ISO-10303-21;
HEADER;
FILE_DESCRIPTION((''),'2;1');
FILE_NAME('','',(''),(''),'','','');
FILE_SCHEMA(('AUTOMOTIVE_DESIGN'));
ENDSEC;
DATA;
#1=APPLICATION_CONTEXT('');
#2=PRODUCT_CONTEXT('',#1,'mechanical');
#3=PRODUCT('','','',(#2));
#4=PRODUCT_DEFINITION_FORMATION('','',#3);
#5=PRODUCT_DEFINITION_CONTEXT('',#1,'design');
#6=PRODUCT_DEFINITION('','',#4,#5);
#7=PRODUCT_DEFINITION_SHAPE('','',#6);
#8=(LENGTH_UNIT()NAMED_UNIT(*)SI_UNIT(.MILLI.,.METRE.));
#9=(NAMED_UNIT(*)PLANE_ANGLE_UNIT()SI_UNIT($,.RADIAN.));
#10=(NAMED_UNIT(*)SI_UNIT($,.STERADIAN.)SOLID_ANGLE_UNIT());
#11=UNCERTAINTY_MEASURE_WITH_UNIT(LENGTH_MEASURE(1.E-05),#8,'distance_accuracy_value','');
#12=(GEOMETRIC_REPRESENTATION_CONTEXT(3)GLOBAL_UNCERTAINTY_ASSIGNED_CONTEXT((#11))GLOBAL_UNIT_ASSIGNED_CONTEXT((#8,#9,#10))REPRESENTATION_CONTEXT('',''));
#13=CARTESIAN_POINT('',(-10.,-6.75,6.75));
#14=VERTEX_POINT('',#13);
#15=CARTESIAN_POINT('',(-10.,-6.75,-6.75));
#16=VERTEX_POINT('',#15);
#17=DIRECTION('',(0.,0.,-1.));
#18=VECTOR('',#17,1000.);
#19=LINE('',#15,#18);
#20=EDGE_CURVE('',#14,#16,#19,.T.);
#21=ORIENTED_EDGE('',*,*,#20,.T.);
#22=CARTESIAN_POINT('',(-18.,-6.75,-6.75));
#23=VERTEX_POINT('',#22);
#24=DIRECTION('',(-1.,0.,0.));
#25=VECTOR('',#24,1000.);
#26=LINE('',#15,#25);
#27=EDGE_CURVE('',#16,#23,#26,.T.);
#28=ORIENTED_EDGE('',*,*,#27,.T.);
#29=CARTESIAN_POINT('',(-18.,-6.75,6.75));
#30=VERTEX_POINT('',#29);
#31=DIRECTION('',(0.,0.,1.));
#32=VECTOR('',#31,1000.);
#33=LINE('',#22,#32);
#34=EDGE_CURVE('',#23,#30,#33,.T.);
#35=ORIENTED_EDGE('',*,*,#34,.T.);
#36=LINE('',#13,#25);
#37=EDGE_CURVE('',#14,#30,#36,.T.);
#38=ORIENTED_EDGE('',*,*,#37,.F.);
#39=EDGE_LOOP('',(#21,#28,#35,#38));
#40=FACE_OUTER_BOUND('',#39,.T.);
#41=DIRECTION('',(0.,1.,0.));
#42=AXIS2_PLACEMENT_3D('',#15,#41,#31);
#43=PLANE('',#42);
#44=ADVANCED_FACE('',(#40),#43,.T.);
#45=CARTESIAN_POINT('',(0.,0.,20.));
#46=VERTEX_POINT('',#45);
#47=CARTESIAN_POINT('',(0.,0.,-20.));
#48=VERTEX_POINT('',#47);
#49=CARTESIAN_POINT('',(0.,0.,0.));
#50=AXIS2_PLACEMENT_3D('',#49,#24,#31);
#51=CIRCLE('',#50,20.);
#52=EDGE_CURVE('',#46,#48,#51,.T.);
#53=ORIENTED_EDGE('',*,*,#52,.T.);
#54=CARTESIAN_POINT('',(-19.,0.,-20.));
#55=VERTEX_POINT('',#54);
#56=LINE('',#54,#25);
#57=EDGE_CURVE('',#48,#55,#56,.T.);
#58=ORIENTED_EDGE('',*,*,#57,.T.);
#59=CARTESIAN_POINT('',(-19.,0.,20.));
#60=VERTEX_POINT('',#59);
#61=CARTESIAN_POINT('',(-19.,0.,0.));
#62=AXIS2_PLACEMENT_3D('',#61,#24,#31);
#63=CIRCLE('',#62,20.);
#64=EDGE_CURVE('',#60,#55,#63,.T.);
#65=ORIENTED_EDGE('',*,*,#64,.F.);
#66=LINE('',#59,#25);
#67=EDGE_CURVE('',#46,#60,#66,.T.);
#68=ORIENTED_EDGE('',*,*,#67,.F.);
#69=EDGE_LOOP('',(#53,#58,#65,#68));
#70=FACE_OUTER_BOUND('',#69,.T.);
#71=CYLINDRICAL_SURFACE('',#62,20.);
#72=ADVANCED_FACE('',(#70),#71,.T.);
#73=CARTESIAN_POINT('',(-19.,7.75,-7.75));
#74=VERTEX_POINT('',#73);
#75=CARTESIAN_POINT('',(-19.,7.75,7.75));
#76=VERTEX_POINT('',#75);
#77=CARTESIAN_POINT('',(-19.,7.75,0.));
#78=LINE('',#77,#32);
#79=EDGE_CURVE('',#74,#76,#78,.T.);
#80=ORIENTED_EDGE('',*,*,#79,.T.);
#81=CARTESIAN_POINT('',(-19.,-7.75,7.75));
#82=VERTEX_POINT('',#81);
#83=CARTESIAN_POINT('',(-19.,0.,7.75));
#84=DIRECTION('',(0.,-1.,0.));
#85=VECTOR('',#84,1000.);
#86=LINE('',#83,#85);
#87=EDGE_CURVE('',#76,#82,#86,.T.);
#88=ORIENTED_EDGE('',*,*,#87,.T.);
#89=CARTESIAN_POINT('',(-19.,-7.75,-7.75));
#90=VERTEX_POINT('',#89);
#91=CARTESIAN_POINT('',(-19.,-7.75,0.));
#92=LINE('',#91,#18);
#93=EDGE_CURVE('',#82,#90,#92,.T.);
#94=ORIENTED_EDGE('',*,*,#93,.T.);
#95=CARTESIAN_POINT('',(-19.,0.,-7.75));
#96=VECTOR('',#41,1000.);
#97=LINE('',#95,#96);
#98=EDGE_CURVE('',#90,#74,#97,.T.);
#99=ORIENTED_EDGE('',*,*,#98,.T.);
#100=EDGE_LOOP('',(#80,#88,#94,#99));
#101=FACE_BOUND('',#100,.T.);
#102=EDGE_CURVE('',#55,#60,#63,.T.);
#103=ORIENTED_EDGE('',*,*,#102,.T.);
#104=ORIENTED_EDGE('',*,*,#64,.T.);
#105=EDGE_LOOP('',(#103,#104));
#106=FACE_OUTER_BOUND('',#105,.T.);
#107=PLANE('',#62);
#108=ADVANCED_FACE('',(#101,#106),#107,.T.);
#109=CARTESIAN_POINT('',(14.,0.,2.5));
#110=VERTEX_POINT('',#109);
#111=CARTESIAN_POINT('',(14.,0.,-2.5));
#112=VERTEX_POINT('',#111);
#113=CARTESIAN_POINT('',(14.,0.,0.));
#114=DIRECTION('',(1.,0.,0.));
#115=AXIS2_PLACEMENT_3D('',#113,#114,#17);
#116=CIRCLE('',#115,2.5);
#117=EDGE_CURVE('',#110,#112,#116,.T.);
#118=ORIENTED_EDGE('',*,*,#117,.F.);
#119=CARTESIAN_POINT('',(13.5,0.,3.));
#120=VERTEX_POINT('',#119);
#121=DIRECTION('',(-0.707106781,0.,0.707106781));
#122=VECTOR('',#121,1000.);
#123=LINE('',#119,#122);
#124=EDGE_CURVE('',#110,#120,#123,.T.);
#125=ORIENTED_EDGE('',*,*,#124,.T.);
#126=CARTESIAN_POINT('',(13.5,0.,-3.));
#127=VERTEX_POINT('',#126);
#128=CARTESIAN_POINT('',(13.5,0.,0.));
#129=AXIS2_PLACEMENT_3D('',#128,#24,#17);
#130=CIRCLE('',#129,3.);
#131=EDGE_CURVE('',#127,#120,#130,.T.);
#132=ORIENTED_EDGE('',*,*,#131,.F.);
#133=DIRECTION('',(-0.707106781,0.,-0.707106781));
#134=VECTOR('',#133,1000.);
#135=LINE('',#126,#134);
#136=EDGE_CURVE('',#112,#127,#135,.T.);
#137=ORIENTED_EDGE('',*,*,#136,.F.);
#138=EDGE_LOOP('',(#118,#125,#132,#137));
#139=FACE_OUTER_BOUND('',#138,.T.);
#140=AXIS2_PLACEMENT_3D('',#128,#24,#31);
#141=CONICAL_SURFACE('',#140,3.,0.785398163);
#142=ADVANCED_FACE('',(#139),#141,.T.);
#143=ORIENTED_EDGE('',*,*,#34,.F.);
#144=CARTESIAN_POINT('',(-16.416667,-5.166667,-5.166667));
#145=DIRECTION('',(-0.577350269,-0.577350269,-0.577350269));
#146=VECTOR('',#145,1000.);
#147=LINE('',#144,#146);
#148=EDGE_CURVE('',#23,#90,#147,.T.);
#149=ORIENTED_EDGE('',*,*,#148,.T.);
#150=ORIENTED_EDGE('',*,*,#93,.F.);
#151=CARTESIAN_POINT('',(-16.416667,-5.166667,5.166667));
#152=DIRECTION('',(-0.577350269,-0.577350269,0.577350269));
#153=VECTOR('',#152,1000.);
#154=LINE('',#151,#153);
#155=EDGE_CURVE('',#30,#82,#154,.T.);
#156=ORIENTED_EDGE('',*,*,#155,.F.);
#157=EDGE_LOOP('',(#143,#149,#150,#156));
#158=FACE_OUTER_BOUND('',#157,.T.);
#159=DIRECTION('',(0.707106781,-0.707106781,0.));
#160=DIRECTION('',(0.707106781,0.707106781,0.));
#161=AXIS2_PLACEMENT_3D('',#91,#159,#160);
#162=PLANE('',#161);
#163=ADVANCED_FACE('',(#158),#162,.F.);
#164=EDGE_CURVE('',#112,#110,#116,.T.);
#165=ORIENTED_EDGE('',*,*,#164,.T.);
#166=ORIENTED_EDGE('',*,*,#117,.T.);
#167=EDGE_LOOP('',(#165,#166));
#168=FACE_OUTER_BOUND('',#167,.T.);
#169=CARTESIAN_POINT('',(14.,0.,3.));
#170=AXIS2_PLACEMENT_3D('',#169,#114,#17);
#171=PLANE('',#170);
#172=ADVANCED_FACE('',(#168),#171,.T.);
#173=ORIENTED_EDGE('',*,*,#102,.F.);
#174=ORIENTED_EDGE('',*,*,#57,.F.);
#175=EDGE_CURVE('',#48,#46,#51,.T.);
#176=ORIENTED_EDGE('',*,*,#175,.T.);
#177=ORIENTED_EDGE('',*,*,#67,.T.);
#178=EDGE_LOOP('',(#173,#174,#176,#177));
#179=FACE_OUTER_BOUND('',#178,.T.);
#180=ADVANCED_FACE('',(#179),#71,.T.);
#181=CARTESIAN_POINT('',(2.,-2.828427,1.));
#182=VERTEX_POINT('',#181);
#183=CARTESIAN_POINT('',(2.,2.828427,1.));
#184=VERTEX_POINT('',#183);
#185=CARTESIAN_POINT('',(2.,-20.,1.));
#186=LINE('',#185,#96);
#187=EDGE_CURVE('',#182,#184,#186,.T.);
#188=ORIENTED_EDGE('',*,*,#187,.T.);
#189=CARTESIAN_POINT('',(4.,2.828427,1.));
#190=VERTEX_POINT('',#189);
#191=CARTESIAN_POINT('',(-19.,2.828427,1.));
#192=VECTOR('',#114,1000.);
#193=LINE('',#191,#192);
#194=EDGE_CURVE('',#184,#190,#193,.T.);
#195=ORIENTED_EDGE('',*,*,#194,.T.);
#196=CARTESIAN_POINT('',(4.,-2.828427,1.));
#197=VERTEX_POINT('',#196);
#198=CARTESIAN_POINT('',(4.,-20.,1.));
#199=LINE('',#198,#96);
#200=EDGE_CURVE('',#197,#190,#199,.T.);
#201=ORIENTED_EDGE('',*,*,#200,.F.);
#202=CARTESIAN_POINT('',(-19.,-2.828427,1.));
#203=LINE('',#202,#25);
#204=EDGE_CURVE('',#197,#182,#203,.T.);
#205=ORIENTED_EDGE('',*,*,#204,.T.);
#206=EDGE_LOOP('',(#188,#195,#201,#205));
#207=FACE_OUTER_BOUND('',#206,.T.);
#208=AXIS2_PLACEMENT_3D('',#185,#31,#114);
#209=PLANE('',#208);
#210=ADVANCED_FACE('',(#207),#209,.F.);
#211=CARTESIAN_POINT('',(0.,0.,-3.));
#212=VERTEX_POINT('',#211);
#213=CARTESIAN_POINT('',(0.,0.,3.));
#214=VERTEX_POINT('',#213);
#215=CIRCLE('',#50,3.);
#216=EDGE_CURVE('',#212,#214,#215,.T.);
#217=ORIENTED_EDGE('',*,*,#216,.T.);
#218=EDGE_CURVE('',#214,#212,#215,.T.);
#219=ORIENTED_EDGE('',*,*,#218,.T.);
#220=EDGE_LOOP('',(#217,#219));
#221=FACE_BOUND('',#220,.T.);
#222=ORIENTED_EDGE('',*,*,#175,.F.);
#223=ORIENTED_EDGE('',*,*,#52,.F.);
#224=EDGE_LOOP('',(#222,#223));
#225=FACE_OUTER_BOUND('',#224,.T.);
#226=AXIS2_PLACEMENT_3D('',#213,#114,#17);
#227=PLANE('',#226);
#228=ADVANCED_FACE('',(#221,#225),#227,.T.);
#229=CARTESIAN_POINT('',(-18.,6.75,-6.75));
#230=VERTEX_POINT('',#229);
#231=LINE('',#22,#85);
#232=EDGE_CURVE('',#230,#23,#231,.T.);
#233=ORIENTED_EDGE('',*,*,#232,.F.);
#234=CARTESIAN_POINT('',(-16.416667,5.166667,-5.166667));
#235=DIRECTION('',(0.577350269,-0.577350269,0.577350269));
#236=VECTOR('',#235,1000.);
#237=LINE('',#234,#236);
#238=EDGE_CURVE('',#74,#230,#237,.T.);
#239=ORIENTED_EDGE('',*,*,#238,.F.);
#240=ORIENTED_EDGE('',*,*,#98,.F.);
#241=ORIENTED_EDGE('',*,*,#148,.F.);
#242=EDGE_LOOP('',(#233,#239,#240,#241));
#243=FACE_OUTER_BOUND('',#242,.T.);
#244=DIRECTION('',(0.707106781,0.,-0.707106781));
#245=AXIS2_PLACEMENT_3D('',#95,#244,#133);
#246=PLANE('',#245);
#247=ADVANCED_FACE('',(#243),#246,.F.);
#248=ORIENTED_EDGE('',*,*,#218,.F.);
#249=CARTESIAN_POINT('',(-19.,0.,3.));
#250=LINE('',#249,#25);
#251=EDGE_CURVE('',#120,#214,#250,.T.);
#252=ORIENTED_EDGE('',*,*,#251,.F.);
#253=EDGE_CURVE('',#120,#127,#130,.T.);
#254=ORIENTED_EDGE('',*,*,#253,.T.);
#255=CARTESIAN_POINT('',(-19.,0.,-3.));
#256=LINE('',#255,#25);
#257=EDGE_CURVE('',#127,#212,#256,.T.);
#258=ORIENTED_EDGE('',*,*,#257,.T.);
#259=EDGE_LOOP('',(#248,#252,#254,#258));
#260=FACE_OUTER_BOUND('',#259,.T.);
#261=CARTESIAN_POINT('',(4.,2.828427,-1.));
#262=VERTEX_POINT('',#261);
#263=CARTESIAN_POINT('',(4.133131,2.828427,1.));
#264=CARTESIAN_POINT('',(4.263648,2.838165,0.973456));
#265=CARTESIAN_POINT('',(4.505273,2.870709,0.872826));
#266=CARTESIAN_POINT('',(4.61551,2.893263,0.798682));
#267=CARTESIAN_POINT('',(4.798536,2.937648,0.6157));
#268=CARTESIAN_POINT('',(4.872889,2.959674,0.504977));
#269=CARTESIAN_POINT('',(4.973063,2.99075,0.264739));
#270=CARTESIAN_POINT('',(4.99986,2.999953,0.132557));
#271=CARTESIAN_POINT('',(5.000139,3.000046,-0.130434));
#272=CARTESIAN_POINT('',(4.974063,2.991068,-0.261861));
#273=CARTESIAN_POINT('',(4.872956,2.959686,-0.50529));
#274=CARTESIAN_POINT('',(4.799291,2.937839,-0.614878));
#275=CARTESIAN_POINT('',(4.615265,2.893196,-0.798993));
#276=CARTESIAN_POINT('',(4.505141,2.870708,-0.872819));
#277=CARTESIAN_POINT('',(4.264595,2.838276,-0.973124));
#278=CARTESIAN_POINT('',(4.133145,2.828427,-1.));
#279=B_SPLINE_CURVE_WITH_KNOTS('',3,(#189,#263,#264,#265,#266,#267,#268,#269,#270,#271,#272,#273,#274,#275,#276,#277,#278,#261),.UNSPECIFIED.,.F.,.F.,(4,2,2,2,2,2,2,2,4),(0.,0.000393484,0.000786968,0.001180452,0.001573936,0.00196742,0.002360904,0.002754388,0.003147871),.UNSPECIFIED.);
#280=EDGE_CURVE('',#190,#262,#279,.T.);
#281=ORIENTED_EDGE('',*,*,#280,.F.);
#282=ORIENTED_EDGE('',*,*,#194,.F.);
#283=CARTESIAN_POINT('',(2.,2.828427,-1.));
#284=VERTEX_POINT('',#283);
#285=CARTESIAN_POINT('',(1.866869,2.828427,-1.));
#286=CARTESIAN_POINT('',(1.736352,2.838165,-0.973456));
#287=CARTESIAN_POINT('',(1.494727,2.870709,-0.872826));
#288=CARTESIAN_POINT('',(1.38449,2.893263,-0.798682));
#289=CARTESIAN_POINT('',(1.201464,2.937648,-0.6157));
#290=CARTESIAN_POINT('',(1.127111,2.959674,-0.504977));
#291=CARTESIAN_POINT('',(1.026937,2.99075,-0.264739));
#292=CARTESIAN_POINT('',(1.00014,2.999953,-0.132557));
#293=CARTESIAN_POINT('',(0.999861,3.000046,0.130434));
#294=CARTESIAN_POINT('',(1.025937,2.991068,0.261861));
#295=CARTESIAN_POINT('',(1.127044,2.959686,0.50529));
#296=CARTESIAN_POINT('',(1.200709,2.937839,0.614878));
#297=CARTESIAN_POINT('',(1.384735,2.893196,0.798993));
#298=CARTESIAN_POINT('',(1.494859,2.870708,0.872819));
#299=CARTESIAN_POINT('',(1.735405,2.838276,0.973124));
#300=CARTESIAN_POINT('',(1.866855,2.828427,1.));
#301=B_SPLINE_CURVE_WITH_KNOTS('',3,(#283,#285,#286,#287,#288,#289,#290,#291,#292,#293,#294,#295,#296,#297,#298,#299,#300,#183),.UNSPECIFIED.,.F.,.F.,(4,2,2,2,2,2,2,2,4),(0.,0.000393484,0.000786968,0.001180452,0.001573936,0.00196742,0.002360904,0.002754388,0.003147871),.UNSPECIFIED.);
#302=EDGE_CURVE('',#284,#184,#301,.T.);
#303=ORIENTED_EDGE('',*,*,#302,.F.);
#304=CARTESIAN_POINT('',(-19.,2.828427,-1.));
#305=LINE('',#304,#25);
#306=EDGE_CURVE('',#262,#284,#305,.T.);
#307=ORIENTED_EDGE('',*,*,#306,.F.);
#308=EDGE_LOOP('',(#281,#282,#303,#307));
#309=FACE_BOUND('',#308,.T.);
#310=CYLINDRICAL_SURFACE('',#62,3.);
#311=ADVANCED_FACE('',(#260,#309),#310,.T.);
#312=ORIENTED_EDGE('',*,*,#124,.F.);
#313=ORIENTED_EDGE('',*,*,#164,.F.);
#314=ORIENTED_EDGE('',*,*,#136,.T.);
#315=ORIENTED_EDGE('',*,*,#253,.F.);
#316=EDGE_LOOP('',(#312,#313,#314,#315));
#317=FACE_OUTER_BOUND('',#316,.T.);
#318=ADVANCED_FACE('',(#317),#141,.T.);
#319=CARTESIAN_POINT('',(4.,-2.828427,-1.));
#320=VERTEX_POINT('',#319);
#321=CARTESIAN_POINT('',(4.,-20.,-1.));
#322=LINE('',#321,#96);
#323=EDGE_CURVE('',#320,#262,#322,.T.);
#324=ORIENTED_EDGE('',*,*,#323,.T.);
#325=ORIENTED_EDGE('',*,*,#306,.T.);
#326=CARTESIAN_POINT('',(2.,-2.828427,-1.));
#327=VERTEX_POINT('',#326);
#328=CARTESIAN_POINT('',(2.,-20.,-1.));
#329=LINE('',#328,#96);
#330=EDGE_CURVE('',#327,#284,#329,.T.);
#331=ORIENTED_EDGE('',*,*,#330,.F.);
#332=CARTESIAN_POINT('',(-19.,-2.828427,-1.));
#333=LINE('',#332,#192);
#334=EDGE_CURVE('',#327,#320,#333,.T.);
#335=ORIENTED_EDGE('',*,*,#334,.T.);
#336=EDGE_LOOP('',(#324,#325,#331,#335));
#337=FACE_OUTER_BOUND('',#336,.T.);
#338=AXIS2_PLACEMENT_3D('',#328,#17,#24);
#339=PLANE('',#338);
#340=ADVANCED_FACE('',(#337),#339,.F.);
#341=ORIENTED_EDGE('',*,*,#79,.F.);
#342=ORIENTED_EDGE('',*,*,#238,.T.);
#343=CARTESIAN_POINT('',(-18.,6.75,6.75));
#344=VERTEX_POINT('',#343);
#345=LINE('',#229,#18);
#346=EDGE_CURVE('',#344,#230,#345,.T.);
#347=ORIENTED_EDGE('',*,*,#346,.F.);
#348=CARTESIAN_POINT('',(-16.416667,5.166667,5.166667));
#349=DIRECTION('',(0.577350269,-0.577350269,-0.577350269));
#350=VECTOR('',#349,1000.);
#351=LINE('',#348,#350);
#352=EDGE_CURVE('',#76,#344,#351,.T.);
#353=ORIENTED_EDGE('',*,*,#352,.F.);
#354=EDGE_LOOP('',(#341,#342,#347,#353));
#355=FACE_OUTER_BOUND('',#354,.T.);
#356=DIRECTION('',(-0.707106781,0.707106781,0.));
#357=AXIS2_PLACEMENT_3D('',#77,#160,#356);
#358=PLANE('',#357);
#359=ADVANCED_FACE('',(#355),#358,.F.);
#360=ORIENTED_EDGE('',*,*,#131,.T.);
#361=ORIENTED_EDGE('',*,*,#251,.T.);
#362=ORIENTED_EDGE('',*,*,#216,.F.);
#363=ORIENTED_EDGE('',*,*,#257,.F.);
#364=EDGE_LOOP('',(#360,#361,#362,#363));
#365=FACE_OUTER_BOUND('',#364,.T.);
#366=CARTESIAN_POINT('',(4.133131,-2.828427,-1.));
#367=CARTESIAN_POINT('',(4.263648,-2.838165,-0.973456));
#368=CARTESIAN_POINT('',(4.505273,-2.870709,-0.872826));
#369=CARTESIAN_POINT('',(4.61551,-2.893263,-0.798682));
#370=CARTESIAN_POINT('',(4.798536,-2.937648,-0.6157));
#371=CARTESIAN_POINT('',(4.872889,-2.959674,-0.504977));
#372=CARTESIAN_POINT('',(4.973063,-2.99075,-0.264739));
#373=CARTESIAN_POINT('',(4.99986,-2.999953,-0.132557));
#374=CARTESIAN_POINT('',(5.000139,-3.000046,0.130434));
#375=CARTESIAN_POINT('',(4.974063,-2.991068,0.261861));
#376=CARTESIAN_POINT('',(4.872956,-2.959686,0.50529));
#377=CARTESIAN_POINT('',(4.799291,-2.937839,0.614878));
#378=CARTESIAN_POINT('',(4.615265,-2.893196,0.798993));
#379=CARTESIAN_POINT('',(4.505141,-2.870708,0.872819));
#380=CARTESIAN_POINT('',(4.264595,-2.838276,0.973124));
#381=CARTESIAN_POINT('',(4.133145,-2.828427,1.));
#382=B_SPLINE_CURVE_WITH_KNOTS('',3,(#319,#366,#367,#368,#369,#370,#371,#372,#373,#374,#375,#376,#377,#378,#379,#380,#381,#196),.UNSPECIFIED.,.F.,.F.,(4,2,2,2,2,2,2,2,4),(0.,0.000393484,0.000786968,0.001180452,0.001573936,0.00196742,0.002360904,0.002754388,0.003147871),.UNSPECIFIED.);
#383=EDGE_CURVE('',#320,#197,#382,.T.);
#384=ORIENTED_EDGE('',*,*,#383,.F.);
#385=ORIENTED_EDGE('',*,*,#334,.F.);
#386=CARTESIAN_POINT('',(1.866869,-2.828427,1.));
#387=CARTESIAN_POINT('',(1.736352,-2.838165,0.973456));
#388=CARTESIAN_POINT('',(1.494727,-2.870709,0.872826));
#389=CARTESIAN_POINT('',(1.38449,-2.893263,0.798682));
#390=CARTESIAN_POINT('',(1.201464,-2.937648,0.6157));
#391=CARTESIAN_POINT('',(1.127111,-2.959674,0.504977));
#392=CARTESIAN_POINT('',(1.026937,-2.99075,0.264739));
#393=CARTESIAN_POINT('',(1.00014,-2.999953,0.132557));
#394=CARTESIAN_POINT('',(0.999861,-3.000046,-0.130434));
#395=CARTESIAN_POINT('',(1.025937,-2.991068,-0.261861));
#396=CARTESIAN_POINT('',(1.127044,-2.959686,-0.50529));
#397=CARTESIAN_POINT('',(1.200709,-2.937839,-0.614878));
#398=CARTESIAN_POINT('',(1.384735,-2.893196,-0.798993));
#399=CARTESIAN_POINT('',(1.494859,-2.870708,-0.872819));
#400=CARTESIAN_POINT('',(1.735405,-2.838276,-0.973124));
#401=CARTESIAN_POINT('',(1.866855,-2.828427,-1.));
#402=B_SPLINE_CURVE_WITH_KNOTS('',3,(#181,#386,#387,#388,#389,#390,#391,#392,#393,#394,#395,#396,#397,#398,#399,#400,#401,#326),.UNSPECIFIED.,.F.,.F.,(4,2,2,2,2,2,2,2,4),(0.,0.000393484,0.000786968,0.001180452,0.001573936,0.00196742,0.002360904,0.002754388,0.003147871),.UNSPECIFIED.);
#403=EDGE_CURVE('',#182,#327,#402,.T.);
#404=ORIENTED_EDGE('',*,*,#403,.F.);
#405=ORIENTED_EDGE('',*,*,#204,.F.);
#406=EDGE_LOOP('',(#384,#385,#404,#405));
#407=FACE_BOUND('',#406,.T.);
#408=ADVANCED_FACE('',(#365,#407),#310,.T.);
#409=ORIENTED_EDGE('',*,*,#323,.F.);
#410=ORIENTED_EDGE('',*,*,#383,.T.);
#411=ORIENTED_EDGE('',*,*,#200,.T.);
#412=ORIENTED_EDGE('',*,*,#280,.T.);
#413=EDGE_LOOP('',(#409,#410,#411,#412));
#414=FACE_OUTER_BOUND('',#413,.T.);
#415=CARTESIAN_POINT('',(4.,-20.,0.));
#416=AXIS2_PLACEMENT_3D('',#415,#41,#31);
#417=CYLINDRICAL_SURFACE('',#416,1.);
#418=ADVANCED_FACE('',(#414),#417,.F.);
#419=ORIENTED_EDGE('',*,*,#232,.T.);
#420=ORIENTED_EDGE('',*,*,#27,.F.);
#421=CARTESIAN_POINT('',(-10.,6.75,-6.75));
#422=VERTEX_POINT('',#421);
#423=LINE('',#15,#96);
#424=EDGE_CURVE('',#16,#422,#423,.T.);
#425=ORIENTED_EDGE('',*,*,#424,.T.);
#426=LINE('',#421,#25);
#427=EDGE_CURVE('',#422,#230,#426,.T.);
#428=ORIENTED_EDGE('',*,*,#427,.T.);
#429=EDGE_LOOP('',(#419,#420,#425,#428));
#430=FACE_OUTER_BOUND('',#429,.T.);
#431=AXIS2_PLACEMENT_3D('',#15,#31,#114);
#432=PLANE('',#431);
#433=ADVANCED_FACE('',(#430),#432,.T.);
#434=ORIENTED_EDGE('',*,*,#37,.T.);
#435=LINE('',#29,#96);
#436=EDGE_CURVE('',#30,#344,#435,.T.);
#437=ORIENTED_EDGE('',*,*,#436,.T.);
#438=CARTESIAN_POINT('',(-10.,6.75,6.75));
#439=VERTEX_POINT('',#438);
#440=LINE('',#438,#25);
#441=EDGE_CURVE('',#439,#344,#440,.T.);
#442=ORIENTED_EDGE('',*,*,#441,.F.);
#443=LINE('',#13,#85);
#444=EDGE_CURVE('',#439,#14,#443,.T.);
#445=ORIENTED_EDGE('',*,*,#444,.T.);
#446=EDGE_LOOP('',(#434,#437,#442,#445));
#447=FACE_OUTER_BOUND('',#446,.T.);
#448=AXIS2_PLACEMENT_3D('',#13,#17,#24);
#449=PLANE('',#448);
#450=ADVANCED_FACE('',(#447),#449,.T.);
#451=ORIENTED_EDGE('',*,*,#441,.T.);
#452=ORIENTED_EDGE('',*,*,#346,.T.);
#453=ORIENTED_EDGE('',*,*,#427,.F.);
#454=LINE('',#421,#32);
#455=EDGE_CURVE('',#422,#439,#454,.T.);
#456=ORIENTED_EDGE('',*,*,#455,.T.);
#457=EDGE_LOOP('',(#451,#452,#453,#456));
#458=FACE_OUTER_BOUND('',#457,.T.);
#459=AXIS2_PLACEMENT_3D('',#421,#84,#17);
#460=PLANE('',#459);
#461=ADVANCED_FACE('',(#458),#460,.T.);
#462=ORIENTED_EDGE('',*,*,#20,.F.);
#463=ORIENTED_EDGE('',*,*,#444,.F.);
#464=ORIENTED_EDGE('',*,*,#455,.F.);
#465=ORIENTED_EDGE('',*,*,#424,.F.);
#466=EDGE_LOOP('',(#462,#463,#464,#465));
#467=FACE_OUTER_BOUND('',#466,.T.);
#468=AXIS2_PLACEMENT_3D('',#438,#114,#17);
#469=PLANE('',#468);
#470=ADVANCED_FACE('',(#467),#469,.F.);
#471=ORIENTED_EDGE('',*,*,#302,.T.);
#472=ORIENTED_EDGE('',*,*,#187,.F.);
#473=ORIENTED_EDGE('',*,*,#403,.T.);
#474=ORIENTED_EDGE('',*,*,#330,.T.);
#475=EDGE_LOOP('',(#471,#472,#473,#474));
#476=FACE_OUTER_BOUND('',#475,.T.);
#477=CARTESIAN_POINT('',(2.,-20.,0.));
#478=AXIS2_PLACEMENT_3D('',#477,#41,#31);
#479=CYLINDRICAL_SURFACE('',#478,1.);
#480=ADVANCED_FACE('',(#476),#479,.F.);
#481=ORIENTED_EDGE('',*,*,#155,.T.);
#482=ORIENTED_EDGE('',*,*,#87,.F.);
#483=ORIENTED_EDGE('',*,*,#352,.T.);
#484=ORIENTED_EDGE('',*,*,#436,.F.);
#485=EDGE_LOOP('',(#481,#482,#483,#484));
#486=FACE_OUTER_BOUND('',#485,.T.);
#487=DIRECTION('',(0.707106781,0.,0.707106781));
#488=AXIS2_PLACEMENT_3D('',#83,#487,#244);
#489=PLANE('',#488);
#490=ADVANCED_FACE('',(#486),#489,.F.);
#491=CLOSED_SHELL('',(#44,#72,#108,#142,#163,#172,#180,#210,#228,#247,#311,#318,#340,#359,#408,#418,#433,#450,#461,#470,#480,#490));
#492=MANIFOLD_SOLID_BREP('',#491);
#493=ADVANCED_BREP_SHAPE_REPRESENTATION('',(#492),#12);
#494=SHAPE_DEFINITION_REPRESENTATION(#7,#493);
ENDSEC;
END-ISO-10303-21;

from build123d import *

# Parameters (mm, degrees)
SKETCH2_W               = 13.5
SKETCH2_H               = 13.5
CUT_EXTRUDE1_DEPTH      = 9
CHAMFER1_SIZE           = 1
CUT_EXTRUDE2_DEPTH      = 35.073450075
CUT_EXTRUDE2_DEPTH_BACK = 35.073450075
CHAMFER2_SIZE           = 0.5


with BuildPart() as part:
    # Sketch1 → Revolve1 (revolve)
    with BuildSketch(Plane(origin=(0, 0, 0), x_dir=(1, 0, 0), z_dir=(0, 1, 0))):
        Polygon((0, -3), (14, -3), (14, 0), (-19, 0), (-19, -20), (0, -20), align=None)
    revolve(axis=Axis((-19, 0, 0), (1, 0, 0)))

    # Sketch2 → Cut-Extrude1 (cut)
    with BuildSketch(Plane(origin=(-19, 0, 0), x_dir=(0, 0, -1), z_dir=(1, 0, 0))):
        Rectangle(SKETCH2_W, SKETCH2_H)
    extrude(amount=CUT_EXTRUDE1_DEPTH, mode=Mode.SUBTRACT)

    # Chamfer1
    chamfer1_edges = [part.edges().sort_by_distance(p)[0] for p in [
        (-19, 0, 6.75),
        (-19, -6.75, 0),
        (-19, 0, -6.75),
        (-19, 6.75, 0),
    ]]
    chamfer(chamfer1_edges, length=CHAMFER1_SIZE)

    # Sketch3 → Cut-Extrude2 (cut, two sides: drawn at the far end of the back side and taken through both)
    with BuildSketch(Plane(origin=(0, 0, 0), x_dir=(1, 0, 0), z_dir=(0, 1, 0)).offset(-CUT_EXTRUDE2_DEPTH_BACK)):
        with BuildLine():
            Line((2, 1), (4, 1))
            ThreePointArc((4, 1), (5, 0), (4, -1))
            Line((4, -1), (2, -1))
            ThreePointArc((2, -1), (1, 0), (2, 1))
        make_face()
    extrude(amount=CUT_EXTRUDE2_DEPTH + CUT_EXTRUDE2_DEPTH_BACK, mode=Mode.SUBTRACT)

    # Chamfer2
    chamfer2_edges = [part.edges().sort_by_distance(p)[0] for p in [
        (14, 0, -3),
    ]]
    chamfer(chamfer2_edges, length=CHAMFER2_SIZE)


solid = part.part
